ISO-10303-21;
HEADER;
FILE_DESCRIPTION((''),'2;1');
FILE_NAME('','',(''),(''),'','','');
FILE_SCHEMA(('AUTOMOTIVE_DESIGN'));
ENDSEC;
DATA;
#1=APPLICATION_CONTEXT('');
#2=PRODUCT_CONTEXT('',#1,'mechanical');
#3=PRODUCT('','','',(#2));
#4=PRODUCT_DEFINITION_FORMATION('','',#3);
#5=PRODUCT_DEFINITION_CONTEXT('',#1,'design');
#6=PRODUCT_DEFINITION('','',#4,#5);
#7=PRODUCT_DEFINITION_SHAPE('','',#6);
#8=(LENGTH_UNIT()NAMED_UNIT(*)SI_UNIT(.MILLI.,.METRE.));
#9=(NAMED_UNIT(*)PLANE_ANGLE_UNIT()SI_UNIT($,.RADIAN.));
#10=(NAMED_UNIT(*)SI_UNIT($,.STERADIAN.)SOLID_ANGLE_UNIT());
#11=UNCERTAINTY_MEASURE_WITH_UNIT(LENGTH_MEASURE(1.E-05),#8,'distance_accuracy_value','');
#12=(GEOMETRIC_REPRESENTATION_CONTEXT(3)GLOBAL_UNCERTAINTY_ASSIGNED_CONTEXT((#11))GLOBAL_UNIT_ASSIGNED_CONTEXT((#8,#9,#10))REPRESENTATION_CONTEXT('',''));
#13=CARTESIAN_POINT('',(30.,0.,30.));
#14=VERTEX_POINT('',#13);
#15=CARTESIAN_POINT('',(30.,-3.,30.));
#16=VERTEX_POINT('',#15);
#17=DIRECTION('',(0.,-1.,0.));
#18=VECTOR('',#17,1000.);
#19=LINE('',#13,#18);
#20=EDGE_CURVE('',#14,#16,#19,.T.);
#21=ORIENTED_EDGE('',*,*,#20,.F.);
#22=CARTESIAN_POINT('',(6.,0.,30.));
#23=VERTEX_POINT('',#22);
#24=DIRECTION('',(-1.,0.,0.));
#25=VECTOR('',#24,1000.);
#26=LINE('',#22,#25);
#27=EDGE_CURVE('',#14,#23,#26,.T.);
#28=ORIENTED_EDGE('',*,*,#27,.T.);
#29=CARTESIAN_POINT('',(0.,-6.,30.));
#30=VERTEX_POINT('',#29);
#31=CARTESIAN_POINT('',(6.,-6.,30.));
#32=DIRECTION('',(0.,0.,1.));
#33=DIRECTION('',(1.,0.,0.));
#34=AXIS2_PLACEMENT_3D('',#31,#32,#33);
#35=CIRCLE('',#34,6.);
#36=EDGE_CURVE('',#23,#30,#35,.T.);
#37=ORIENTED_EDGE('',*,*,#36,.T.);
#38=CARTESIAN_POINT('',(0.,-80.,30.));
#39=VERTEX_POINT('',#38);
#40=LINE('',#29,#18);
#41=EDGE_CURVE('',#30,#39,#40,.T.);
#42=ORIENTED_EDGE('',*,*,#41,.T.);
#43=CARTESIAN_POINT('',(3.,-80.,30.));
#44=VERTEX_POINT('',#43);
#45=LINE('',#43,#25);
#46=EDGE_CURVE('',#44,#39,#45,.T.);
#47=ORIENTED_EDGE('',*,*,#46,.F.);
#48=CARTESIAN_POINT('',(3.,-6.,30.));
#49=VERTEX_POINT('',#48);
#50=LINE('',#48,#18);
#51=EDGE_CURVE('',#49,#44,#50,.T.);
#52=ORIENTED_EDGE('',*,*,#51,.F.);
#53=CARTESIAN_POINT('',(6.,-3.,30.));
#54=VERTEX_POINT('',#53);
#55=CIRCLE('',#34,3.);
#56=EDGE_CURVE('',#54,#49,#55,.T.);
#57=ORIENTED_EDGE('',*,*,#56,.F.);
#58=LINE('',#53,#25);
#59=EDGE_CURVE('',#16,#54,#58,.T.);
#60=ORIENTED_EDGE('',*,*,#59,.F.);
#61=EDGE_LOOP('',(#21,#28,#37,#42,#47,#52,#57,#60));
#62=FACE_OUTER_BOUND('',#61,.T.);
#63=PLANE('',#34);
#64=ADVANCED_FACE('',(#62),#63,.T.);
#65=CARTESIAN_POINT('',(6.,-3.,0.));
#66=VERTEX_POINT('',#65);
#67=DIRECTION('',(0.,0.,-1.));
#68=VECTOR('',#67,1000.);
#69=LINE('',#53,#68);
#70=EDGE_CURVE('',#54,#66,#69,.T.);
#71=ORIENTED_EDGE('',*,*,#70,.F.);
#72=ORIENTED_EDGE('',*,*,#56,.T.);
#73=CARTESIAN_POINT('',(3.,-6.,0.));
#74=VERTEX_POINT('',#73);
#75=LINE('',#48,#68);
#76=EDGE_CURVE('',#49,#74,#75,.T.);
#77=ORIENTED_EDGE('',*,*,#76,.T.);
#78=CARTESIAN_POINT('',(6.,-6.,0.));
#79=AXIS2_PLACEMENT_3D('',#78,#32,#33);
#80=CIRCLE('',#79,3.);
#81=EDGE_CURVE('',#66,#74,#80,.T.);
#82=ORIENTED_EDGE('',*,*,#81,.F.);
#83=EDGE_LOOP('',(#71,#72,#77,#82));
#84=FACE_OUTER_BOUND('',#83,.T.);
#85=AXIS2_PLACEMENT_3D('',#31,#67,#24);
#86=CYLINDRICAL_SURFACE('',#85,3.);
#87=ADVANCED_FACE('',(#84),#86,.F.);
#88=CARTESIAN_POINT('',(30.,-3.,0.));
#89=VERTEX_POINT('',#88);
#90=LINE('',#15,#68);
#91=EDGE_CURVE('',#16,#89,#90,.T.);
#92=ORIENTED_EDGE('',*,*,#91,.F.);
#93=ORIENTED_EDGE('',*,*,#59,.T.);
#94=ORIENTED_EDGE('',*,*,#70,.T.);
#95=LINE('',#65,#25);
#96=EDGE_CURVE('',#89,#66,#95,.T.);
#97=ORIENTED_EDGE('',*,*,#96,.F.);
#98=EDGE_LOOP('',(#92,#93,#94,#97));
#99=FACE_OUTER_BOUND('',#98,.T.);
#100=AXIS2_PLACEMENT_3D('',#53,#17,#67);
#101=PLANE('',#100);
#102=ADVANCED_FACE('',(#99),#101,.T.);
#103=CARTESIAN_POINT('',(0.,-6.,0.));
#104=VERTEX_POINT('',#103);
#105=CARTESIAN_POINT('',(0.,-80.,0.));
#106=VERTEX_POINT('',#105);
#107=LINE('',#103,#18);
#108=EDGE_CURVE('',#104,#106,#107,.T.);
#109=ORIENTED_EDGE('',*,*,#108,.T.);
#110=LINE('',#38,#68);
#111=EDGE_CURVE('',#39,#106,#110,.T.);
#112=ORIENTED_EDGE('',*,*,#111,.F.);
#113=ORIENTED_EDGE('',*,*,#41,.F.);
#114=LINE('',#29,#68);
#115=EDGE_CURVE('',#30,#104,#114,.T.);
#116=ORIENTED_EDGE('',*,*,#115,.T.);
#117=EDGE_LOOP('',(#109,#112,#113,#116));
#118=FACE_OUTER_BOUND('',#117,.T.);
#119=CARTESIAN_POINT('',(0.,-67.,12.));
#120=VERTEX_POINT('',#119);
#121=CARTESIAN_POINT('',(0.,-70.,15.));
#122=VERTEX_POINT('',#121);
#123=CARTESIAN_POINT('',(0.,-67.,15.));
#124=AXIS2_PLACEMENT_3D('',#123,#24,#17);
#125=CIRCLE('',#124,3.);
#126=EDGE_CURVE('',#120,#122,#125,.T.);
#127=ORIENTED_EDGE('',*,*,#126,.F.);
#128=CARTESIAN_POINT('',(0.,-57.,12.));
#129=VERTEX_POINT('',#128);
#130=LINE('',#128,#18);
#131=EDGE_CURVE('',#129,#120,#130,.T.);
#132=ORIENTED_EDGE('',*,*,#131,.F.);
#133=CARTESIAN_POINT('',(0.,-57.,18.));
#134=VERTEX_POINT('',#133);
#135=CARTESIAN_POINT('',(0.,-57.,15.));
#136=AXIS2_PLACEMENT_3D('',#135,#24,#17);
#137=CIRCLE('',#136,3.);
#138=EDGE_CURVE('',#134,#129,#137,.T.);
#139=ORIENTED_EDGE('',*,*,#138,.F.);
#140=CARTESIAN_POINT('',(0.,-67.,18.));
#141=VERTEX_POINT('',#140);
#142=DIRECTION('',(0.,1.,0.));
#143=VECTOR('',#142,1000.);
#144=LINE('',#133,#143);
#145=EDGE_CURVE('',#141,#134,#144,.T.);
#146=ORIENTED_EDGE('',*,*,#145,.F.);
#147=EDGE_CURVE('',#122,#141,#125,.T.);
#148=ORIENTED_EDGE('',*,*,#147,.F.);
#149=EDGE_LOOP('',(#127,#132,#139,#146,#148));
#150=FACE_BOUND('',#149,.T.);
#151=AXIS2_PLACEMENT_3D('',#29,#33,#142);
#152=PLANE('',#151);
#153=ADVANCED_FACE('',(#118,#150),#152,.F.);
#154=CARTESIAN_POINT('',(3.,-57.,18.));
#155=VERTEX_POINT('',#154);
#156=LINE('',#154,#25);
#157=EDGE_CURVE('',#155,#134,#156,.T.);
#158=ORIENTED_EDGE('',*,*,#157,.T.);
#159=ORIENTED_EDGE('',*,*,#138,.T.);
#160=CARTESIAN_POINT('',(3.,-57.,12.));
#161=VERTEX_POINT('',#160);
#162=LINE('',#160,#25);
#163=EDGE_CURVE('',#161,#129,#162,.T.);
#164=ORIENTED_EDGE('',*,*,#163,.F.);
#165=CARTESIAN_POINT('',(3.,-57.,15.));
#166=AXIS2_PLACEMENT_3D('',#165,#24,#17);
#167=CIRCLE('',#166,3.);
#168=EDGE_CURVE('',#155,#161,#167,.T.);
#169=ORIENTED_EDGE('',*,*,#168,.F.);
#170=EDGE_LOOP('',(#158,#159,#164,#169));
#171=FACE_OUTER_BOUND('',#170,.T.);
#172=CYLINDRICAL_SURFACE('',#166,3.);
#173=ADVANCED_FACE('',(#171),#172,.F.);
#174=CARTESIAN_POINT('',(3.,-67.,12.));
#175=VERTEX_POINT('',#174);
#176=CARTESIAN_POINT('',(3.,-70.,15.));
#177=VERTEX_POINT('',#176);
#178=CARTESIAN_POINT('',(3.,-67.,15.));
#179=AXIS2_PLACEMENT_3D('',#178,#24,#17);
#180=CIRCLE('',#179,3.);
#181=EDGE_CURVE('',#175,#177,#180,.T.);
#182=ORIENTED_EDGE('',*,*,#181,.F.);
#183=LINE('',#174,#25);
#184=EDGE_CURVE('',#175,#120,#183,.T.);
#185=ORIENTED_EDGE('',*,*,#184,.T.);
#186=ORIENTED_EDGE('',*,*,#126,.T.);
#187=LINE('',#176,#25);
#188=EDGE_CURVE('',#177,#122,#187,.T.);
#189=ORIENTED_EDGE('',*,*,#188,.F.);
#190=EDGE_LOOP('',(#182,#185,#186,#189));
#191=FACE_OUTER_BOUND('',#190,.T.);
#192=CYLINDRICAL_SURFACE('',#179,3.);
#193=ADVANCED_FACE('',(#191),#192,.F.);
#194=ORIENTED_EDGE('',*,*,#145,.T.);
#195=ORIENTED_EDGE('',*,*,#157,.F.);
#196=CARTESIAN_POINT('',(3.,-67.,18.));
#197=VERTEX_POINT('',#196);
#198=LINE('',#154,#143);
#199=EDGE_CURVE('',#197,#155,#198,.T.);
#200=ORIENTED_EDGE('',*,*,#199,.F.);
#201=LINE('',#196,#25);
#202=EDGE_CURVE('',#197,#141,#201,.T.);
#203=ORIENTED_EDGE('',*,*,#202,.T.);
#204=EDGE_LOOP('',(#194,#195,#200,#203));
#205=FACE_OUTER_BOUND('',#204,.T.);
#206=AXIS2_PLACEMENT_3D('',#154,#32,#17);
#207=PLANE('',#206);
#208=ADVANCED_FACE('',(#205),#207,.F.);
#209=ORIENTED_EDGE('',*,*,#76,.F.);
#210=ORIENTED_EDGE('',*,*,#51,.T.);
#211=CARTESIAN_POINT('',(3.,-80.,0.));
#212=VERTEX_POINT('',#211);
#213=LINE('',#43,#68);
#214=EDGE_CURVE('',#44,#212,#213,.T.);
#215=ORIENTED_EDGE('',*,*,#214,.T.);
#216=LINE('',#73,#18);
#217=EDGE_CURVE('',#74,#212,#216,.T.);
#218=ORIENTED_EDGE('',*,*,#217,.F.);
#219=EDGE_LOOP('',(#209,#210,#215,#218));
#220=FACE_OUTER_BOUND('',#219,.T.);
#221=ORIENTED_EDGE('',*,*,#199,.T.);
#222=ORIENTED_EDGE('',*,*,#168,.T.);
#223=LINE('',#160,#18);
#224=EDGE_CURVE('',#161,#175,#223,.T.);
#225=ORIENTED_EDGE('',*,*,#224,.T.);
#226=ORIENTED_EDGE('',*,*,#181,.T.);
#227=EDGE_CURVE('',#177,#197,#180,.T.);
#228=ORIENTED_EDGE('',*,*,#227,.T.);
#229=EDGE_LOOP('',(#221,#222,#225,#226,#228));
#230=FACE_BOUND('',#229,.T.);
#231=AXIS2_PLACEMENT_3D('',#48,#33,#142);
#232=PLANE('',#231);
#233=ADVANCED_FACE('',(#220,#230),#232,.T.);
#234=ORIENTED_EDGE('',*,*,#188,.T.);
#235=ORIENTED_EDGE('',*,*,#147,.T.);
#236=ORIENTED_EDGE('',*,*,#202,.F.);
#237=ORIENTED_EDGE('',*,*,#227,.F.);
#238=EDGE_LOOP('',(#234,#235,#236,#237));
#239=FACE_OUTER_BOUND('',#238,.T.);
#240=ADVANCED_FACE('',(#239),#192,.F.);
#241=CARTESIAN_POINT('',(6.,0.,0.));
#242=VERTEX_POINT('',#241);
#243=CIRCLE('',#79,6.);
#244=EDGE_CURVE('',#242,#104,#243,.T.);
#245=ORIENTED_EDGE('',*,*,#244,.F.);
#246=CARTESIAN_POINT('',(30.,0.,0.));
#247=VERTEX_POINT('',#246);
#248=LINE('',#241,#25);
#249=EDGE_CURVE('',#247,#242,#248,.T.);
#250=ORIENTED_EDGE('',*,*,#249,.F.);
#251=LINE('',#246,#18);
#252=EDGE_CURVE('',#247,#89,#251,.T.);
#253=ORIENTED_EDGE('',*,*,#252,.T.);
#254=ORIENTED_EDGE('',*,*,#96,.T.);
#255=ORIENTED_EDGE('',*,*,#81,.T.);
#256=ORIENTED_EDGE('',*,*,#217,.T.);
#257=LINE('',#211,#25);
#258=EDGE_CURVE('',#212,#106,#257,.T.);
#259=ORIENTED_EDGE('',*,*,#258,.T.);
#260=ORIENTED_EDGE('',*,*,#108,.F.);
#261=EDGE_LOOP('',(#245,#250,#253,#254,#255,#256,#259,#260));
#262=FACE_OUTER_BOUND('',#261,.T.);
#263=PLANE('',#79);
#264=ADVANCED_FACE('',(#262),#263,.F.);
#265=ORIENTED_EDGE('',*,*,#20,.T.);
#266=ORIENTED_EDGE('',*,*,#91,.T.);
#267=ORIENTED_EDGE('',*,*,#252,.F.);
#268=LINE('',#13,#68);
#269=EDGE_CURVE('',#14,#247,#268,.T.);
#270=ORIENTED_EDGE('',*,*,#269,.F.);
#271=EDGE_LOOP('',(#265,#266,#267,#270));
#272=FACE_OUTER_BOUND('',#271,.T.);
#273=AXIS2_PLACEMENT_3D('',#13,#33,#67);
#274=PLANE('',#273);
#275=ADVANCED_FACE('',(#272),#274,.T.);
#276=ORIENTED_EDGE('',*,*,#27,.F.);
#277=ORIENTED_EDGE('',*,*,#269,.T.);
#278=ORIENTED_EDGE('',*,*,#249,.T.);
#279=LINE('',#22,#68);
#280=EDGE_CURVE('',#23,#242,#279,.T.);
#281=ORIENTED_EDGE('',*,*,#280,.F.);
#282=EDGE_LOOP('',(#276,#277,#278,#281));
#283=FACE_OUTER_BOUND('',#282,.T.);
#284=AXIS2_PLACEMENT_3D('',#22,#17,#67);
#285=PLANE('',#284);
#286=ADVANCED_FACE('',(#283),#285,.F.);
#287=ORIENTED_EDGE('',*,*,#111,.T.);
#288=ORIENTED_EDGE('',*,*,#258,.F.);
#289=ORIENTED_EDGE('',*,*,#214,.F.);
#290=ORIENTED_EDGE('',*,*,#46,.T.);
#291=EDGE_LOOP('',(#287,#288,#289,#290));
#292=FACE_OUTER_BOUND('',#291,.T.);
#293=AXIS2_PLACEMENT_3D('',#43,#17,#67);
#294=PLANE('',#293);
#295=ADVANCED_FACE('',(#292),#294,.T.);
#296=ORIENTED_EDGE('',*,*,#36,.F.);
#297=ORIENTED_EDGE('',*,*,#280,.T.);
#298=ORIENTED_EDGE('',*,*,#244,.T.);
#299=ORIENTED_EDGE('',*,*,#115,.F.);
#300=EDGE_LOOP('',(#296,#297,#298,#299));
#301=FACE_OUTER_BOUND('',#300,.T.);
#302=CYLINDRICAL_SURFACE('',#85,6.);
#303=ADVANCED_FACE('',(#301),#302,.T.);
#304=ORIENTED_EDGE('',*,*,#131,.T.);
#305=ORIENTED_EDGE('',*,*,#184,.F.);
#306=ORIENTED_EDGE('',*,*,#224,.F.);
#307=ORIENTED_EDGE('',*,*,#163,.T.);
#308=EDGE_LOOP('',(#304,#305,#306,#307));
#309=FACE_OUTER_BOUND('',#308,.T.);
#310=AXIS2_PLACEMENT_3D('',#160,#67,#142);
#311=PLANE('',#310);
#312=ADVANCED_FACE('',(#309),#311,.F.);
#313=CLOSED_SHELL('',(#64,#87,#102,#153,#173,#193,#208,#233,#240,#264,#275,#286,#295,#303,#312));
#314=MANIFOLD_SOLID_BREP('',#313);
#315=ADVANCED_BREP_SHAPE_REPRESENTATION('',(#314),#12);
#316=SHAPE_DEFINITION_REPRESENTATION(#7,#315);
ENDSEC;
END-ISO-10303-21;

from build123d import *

# Parameters (mm, degrees)
EXTRUDE_THIN1_DEPTH = 30
CUT_EXTRUDE1_DEPTH  = 3


with BuildPart() as part:
    # Sketch1 → Extrude-Thin1 (new body)
    with BuildSketch(Plane.XY):
        with BuildLine():
            Line((0, -80), (0, -6))
            ThreePointArc((0, -6), (1.757359313, -1.757359313), (6, 0))
            Line((6, 0), (30, 0))
            Line((30, 0), (30, -3))
            Line((30, -3), (6, -3))
            ThreePointArc((6, -3), (3.878679656, -3.878679656), (3, -6))
            Line((3, -6), (3, -80))
            Line((3, -80), (0, -80))
        make_face()
    extrude(amount=EXTRUDE_THIN1_DEPTH)

    # Sketch2 → Cut-Extrude1 (cut)
    with BuildSketch(Plane.ZY):
        with BuildLine():
            Line((18, -57), (18, -67))
            ThreePointArc((18, -67), (15, -70), (12, -67))
            Line((12, -67), (12, -57))
            ThreePointArc((12, -57), (15, -54), (18, -57))
        make_face()
    extrude(amount=-CUT_EXTRUDE1_DEPTH, mode=Mode.SUBTRACT)


solid = part.part
